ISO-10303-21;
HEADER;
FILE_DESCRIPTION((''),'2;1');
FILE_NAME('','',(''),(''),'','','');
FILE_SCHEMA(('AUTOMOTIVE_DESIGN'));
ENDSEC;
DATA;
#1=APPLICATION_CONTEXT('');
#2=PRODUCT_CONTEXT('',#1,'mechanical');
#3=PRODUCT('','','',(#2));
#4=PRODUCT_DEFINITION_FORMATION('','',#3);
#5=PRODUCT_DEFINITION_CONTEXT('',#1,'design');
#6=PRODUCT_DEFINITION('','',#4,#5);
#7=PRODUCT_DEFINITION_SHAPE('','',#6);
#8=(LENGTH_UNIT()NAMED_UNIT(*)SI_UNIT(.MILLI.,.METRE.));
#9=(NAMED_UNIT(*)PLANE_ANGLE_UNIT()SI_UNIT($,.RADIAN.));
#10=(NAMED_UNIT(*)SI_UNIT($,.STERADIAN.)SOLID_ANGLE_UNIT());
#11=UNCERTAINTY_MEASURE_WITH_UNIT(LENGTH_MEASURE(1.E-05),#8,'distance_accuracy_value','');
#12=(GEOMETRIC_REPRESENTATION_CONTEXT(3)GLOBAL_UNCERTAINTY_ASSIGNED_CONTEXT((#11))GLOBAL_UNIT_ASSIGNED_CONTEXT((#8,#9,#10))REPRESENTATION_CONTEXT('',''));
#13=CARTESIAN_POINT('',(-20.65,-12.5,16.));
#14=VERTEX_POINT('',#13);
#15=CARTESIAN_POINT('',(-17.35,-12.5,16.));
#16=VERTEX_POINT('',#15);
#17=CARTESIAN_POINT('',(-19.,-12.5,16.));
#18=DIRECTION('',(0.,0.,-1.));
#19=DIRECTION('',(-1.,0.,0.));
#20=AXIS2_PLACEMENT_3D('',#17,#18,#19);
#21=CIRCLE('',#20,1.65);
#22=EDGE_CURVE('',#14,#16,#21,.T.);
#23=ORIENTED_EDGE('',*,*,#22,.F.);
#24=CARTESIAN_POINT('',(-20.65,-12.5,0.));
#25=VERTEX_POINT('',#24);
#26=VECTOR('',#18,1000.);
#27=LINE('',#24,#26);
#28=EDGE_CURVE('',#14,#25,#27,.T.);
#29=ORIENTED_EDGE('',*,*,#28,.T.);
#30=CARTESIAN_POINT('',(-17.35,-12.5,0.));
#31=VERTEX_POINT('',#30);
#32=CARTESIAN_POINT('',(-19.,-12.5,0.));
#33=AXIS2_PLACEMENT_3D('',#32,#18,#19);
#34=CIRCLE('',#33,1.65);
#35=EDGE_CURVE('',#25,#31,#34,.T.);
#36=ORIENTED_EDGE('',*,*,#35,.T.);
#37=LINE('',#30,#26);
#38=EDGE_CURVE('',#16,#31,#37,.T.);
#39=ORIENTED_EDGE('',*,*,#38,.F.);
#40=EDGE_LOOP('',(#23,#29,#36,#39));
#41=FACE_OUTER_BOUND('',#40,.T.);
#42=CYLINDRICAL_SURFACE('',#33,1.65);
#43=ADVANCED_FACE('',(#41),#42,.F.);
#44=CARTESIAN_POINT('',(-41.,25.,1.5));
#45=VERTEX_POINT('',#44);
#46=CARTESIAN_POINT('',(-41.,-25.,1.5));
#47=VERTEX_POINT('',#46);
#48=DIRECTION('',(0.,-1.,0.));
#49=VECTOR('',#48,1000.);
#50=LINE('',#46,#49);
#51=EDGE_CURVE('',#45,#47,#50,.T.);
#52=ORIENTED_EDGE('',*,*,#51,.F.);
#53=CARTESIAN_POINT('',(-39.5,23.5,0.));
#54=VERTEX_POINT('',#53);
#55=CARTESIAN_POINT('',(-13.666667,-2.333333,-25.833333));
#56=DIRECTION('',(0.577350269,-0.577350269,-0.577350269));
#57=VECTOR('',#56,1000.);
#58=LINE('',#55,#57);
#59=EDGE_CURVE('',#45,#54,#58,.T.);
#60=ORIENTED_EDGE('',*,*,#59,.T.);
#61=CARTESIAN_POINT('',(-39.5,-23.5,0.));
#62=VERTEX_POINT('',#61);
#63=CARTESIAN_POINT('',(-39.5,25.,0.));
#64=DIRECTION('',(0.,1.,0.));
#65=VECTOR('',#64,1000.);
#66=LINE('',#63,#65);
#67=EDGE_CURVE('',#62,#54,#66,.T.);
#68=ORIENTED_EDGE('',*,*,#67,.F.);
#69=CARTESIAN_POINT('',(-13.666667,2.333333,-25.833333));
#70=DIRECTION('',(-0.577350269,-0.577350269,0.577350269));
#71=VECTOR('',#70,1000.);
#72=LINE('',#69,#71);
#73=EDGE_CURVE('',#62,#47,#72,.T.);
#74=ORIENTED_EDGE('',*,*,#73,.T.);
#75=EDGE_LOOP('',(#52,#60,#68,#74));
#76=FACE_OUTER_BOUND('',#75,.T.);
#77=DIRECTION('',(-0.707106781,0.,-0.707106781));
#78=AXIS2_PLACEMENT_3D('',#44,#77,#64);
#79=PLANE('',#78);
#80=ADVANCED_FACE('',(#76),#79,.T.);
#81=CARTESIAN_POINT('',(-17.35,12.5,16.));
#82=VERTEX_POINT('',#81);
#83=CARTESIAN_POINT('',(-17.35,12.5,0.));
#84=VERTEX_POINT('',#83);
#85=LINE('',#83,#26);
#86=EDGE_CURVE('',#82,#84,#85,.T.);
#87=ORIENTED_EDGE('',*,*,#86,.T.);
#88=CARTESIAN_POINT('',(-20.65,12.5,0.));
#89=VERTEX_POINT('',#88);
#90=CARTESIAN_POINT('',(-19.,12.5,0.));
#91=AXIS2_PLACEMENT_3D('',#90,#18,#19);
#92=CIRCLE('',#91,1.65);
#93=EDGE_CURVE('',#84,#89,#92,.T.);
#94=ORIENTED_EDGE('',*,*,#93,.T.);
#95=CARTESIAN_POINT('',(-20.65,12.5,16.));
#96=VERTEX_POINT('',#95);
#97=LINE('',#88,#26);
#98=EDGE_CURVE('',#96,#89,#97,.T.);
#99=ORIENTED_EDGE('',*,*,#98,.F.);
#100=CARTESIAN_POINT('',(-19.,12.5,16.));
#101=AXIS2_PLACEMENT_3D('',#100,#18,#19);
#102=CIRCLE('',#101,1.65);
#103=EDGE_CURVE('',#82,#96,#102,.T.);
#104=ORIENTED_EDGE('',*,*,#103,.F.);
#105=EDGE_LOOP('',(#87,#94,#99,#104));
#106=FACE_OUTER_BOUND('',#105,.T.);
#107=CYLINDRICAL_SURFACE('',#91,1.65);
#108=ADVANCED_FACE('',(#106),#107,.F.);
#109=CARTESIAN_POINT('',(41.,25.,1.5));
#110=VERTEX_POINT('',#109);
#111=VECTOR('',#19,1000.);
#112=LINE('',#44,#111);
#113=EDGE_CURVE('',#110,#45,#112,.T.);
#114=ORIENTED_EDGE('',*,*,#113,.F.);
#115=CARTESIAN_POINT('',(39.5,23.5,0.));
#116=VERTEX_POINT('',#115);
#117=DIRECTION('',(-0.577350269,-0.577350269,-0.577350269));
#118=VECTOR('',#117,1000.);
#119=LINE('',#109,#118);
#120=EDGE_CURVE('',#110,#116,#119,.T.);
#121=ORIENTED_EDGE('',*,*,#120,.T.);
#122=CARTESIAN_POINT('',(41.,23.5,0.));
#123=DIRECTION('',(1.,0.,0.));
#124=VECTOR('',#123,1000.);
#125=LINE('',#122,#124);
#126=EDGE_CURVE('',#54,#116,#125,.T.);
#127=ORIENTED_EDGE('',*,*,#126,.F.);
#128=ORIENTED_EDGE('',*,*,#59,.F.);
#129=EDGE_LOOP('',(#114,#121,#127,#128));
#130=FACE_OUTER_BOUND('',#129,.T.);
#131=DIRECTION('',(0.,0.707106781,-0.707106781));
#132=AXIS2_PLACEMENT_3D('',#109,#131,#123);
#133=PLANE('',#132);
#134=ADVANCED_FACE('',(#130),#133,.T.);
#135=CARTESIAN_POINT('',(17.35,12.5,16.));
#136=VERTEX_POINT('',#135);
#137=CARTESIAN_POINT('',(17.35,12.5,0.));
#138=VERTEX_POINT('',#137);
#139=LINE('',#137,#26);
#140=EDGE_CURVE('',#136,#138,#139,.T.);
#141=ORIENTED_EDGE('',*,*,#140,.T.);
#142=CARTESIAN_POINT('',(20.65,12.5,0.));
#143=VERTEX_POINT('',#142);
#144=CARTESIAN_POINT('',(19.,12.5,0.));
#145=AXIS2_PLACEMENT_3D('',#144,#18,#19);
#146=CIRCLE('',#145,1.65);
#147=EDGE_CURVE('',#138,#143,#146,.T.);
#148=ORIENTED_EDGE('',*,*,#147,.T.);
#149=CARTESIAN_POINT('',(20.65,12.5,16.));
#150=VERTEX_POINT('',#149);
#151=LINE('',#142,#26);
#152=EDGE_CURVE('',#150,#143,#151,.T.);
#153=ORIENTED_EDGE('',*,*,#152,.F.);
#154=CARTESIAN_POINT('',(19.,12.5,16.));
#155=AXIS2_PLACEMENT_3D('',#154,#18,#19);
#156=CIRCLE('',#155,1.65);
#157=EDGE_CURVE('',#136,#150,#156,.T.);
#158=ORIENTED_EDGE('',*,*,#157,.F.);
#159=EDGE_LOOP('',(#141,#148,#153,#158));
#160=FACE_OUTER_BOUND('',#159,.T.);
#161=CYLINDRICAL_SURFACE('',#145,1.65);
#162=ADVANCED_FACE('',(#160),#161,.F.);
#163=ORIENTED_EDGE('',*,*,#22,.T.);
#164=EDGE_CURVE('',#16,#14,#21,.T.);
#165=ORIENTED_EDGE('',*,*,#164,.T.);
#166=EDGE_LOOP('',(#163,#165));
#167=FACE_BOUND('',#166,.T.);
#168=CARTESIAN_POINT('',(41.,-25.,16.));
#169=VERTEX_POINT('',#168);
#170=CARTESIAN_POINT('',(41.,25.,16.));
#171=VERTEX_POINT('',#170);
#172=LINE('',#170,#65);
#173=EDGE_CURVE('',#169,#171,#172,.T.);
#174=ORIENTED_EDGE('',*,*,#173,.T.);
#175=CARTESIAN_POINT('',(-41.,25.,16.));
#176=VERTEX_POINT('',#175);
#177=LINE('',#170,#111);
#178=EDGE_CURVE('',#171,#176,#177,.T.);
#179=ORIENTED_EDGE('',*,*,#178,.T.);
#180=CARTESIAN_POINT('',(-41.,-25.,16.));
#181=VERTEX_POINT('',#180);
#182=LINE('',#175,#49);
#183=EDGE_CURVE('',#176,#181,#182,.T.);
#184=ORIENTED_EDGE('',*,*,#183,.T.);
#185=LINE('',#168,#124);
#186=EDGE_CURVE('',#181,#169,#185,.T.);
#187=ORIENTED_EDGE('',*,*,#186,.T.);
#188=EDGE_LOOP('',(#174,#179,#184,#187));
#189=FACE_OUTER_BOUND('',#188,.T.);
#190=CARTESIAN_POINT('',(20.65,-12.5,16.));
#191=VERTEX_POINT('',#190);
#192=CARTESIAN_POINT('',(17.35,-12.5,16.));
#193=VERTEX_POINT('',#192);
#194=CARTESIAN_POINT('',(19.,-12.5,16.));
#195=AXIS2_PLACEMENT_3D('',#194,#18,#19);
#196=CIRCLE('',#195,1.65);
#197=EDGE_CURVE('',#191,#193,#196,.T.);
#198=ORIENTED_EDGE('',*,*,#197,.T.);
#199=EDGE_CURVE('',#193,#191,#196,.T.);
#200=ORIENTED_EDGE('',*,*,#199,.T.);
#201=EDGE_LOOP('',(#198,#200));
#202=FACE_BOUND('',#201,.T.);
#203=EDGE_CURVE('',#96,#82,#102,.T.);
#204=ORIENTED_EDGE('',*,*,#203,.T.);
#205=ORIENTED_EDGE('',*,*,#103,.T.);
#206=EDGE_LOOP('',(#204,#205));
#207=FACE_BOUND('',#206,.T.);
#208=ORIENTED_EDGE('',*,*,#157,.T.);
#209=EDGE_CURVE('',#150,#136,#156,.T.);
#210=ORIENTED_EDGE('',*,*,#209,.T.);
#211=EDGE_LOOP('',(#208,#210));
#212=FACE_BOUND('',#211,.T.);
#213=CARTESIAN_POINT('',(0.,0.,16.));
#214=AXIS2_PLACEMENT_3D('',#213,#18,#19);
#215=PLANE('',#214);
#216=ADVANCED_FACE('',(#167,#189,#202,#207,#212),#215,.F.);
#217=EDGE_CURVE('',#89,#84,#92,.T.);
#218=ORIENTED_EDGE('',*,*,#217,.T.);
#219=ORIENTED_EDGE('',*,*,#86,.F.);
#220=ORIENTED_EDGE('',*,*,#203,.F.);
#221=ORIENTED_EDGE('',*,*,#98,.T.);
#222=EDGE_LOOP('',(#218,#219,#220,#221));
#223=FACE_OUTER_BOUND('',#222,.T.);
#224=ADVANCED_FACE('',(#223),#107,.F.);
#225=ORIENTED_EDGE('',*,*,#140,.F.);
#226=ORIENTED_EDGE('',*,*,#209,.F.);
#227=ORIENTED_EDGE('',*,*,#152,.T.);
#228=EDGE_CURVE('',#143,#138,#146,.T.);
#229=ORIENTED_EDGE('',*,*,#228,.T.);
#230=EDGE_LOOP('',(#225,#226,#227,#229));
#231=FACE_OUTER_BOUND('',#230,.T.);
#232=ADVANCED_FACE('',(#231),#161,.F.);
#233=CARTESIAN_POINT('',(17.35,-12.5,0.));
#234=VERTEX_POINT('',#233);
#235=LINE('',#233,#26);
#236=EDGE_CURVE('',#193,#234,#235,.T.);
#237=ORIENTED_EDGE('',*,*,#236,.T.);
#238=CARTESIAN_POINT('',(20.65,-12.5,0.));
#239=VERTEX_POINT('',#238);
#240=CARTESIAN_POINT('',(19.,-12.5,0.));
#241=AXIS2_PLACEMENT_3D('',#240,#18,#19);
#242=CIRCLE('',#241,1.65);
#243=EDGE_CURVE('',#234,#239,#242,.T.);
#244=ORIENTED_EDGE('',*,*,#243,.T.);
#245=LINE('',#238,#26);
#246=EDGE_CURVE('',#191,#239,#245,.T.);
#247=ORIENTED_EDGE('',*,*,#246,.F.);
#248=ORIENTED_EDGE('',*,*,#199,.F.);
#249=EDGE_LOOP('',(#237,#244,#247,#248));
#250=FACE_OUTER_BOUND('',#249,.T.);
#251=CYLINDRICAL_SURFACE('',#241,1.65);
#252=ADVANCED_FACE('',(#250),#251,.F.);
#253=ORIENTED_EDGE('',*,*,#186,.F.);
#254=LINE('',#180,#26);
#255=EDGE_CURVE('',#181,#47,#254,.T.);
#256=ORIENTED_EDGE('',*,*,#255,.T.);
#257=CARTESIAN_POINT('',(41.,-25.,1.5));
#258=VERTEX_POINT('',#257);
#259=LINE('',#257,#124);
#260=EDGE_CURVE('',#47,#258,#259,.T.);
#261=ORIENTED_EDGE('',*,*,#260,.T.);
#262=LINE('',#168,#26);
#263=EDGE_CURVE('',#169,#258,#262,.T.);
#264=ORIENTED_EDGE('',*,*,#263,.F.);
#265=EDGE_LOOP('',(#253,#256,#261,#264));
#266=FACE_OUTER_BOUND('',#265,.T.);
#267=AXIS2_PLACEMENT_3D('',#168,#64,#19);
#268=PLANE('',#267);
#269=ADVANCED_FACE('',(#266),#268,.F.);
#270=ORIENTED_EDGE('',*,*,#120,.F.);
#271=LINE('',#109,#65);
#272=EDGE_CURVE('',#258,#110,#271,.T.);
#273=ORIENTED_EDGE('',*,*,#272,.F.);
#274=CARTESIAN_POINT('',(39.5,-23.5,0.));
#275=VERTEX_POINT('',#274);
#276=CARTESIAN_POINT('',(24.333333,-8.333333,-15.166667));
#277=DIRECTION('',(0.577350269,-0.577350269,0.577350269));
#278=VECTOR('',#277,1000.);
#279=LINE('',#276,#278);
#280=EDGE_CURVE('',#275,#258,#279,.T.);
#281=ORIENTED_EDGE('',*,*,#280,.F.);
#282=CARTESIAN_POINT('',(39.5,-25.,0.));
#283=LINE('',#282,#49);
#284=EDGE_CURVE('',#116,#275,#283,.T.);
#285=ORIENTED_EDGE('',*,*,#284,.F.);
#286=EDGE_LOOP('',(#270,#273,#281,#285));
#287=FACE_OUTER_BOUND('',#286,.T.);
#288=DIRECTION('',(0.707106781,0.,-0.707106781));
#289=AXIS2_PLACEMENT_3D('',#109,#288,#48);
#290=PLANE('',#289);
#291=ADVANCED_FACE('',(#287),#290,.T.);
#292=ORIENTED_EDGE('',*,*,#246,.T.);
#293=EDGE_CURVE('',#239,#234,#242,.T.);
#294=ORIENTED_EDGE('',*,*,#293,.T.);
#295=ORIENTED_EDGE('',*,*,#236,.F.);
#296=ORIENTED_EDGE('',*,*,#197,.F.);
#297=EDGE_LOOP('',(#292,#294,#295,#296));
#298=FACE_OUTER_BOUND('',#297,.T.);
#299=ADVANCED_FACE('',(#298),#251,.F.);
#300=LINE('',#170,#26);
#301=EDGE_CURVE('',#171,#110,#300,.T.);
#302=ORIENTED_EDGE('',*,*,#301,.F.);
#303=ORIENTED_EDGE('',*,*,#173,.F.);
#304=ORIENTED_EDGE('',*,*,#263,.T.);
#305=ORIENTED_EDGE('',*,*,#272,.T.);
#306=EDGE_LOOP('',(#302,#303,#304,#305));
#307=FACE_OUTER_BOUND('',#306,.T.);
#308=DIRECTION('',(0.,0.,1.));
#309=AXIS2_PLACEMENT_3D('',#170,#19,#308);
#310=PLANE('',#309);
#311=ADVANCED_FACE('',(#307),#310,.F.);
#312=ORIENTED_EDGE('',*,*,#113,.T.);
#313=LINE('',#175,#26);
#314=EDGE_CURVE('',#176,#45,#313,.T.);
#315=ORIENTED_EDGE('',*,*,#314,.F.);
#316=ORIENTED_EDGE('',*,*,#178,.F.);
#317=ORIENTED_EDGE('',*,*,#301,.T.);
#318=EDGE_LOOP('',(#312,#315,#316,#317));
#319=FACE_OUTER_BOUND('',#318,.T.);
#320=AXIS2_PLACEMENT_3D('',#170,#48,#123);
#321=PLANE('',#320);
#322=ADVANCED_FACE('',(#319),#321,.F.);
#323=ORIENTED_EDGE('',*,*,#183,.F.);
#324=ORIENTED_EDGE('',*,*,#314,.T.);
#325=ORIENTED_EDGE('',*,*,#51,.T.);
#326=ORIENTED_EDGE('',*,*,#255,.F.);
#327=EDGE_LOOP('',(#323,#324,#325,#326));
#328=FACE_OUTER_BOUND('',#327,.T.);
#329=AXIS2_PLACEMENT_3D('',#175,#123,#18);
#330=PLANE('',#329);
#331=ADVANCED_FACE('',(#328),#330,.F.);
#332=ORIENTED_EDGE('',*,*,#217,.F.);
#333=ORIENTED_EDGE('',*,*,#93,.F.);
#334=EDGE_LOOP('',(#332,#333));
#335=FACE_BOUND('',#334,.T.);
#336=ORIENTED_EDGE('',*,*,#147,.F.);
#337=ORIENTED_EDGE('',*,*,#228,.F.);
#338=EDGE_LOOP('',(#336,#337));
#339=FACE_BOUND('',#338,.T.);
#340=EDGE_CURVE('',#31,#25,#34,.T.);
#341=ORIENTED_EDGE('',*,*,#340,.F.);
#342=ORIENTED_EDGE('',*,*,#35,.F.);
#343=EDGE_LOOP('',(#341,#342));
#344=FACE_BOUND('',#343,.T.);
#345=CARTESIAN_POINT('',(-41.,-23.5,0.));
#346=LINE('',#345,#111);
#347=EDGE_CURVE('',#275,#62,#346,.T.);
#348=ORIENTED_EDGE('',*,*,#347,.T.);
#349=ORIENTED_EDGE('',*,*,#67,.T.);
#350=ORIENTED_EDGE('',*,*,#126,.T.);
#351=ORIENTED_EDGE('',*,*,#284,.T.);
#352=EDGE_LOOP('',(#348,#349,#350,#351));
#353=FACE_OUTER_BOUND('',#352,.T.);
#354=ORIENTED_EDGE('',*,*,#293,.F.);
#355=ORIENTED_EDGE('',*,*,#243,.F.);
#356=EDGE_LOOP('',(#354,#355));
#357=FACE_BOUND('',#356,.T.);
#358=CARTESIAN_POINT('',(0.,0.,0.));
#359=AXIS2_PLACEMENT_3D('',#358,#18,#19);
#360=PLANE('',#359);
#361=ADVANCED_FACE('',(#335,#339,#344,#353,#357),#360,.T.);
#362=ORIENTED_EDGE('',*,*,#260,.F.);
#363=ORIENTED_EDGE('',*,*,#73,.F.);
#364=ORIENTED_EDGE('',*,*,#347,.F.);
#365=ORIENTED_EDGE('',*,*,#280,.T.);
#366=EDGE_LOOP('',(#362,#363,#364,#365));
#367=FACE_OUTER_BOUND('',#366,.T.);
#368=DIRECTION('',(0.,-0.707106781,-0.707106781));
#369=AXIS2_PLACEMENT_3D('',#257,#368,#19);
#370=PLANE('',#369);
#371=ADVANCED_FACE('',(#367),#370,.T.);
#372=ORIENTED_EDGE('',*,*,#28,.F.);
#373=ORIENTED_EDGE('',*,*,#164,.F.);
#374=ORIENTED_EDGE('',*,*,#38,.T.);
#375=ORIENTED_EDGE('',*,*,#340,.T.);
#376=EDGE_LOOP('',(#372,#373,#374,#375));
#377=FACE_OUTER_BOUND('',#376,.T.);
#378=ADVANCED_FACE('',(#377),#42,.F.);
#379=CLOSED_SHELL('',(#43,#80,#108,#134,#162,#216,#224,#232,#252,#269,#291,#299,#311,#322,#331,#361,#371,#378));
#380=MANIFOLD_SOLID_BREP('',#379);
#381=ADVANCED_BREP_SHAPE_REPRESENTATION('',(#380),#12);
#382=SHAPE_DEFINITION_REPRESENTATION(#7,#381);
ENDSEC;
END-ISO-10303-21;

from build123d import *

# Parameters (mm, degrees)
SKETCH1_W            = 82
SKETCH1_H            = 50
BOSS_EXTRUDE1_DEPTH  = 16
M4_TAPPED_HOLE1_D    = 3.3
LPATTERN1_COUNT      = 2
LPATTERN1_PITCH      = 38
LPATTERN1_COUNT_DIR2 = 2
LPATTERN1_PITCH_DIR2 = 25
CHAMFER1_SIZE        = 1.5


with BuildPart() as part:
    # Sketch1 → Boss-Extrude1 (new body)
    with BuildSketch(Plane.XY):
        Rectangle(SKETCH1_W, SKETCH1_H)
    extrude(amount=BOSS_EXTRUDE1_DEPTH)

    # M4 Tapped Hole1 (through all)
    with Locations(Plane(origin=(19, 12.5, 0), x_dir=(-1, 0, 0), z_dir=(0, 0, -1))):
        with Locations((0, 0)):
            m4_tapped_hole1 = Hole(M4_TAPPED_HOLE1_D / 2)

    # LPattern1: M4 Tapped Hole1 2 × 2
    with Locations(*[(-i * LPATTERN1_PITCH, -j * LPATTERN1_PITCH_DIR2, 0) for i in range(LPATTERN1_COUNT) for j in range(LPATTERN1_COUNT_DIR2) if (i, j) != (0, 0)]):
        add(m4_tapped_hole1, mode=Mode.SUBTRACT)

    # Chamfer1
    chamfer1_edges = [part.edges().sort_by_distance(p)[0] for p in [
        (0, 25, 0),
        (41, 0, 0),
        (0, -25, 0),
        (-41, 0, 0),
    ]]
    chamfer(chamfer1_edges, length=CHAMFER1_SIZE)


solid = part.part
